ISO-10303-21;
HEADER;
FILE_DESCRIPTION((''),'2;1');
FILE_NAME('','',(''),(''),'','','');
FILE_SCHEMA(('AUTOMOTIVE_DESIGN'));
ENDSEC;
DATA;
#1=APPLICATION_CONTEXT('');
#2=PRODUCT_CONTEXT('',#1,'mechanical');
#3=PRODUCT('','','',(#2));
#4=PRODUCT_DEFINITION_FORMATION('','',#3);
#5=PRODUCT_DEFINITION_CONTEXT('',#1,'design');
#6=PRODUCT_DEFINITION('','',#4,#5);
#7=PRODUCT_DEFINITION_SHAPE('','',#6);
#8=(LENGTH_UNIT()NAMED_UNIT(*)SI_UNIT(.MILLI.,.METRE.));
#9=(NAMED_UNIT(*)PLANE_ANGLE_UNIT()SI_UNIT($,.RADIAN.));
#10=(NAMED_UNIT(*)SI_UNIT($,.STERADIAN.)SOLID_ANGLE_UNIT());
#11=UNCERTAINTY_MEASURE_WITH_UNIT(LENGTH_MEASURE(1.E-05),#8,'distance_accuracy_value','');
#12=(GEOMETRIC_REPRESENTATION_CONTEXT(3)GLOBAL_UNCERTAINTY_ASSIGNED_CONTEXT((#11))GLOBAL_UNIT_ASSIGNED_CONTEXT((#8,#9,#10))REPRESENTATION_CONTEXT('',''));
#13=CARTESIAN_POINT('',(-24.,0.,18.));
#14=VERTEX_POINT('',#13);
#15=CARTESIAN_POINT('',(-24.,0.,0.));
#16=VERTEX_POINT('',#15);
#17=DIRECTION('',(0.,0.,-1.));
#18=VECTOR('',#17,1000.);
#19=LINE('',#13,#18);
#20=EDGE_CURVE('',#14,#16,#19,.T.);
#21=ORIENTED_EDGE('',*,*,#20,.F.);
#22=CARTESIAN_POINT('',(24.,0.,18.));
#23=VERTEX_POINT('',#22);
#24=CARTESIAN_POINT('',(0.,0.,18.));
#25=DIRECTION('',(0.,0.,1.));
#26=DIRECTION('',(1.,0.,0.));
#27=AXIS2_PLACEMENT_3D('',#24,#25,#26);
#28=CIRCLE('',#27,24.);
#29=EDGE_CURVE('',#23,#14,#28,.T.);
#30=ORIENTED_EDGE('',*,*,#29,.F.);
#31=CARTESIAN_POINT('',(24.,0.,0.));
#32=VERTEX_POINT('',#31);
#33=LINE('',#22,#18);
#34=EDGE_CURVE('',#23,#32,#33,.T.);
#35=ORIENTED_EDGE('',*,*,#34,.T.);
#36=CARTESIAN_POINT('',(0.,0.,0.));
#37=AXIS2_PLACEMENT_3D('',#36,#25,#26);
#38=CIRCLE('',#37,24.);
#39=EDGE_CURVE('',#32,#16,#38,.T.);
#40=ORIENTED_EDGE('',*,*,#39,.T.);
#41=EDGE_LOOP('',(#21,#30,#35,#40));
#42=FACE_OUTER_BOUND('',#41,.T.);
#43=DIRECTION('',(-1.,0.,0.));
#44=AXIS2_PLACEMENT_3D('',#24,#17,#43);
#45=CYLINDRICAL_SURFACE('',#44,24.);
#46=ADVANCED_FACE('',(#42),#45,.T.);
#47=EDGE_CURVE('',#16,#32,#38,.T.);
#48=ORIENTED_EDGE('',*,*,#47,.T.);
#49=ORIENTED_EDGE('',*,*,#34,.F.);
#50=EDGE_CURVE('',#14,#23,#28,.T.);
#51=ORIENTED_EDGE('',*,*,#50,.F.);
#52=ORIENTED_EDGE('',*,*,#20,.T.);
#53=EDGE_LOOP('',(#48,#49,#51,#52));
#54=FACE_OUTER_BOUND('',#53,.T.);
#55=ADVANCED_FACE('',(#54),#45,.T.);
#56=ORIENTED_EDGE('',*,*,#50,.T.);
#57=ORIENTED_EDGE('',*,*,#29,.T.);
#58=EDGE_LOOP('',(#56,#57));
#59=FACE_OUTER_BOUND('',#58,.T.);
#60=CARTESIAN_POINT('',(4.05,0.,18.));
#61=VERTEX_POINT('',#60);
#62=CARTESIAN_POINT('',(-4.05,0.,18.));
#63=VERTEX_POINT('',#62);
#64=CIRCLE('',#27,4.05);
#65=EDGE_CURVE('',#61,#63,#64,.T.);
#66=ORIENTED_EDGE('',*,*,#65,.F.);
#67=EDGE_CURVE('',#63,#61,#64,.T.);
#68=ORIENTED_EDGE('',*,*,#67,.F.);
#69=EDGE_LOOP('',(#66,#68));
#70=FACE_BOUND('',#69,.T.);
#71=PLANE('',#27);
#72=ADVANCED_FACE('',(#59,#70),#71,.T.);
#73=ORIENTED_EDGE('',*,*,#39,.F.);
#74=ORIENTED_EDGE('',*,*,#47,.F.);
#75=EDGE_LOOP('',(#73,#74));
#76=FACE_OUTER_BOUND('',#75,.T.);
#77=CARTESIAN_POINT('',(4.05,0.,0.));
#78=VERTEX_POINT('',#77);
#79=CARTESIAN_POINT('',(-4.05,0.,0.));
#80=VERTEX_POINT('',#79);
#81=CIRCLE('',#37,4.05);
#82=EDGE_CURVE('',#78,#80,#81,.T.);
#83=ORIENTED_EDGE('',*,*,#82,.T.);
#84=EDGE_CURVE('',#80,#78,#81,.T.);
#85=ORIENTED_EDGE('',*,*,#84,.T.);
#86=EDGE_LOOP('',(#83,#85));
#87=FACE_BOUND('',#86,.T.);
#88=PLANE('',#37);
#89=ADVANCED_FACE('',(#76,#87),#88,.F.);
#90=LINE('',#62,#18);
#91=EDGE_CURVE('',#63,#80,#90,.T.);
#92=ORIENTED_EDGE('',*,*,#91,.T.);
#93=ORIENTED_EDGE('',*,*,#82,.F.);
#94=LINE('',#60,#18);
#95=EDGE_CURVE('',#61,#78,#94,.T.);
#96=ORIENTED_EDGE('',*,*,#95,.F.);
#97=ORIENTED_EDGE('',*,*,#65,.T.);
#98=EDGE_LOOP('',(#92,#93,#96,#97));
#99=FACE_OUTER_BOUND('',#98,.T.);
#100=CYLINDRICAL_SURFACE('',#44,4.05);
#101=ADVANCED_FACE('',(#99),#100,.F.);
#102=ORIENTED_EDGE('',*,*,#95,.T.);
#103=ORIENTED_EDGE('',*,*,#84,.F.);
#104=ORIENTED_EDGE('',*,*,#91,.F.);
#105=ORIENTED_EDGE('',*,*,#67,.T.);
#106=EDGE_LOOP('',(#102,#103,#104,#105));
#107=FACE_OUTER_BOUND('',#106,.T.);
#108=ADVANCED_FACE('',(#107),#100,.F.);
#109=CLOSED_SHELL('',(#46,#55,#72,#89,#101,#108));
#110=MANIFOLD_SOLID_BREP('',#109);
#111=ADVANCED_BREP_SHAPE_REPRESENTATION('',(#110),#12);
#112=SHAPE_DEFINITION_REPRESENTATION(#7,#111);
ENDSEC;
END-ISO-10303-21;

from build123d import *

# Parameters (mm, degrees)
SKETCH_1_R      = 24
SKETCH_1_R_2    = 4.05
EXTRUDE_1_DEPTH = 18


with BuildPart() as part:
    # 草图1 → 凸台-拉伸1 (new body)
    with BuildSketch(Plane.XY):
        Circle(SKETCH_1_R)
        Circle(SKETCH_1_R_2, mode=Mode.SUBTRACT)
    extrude(amount=EXTRUDE_1_DEPTH)


solid = part.part
